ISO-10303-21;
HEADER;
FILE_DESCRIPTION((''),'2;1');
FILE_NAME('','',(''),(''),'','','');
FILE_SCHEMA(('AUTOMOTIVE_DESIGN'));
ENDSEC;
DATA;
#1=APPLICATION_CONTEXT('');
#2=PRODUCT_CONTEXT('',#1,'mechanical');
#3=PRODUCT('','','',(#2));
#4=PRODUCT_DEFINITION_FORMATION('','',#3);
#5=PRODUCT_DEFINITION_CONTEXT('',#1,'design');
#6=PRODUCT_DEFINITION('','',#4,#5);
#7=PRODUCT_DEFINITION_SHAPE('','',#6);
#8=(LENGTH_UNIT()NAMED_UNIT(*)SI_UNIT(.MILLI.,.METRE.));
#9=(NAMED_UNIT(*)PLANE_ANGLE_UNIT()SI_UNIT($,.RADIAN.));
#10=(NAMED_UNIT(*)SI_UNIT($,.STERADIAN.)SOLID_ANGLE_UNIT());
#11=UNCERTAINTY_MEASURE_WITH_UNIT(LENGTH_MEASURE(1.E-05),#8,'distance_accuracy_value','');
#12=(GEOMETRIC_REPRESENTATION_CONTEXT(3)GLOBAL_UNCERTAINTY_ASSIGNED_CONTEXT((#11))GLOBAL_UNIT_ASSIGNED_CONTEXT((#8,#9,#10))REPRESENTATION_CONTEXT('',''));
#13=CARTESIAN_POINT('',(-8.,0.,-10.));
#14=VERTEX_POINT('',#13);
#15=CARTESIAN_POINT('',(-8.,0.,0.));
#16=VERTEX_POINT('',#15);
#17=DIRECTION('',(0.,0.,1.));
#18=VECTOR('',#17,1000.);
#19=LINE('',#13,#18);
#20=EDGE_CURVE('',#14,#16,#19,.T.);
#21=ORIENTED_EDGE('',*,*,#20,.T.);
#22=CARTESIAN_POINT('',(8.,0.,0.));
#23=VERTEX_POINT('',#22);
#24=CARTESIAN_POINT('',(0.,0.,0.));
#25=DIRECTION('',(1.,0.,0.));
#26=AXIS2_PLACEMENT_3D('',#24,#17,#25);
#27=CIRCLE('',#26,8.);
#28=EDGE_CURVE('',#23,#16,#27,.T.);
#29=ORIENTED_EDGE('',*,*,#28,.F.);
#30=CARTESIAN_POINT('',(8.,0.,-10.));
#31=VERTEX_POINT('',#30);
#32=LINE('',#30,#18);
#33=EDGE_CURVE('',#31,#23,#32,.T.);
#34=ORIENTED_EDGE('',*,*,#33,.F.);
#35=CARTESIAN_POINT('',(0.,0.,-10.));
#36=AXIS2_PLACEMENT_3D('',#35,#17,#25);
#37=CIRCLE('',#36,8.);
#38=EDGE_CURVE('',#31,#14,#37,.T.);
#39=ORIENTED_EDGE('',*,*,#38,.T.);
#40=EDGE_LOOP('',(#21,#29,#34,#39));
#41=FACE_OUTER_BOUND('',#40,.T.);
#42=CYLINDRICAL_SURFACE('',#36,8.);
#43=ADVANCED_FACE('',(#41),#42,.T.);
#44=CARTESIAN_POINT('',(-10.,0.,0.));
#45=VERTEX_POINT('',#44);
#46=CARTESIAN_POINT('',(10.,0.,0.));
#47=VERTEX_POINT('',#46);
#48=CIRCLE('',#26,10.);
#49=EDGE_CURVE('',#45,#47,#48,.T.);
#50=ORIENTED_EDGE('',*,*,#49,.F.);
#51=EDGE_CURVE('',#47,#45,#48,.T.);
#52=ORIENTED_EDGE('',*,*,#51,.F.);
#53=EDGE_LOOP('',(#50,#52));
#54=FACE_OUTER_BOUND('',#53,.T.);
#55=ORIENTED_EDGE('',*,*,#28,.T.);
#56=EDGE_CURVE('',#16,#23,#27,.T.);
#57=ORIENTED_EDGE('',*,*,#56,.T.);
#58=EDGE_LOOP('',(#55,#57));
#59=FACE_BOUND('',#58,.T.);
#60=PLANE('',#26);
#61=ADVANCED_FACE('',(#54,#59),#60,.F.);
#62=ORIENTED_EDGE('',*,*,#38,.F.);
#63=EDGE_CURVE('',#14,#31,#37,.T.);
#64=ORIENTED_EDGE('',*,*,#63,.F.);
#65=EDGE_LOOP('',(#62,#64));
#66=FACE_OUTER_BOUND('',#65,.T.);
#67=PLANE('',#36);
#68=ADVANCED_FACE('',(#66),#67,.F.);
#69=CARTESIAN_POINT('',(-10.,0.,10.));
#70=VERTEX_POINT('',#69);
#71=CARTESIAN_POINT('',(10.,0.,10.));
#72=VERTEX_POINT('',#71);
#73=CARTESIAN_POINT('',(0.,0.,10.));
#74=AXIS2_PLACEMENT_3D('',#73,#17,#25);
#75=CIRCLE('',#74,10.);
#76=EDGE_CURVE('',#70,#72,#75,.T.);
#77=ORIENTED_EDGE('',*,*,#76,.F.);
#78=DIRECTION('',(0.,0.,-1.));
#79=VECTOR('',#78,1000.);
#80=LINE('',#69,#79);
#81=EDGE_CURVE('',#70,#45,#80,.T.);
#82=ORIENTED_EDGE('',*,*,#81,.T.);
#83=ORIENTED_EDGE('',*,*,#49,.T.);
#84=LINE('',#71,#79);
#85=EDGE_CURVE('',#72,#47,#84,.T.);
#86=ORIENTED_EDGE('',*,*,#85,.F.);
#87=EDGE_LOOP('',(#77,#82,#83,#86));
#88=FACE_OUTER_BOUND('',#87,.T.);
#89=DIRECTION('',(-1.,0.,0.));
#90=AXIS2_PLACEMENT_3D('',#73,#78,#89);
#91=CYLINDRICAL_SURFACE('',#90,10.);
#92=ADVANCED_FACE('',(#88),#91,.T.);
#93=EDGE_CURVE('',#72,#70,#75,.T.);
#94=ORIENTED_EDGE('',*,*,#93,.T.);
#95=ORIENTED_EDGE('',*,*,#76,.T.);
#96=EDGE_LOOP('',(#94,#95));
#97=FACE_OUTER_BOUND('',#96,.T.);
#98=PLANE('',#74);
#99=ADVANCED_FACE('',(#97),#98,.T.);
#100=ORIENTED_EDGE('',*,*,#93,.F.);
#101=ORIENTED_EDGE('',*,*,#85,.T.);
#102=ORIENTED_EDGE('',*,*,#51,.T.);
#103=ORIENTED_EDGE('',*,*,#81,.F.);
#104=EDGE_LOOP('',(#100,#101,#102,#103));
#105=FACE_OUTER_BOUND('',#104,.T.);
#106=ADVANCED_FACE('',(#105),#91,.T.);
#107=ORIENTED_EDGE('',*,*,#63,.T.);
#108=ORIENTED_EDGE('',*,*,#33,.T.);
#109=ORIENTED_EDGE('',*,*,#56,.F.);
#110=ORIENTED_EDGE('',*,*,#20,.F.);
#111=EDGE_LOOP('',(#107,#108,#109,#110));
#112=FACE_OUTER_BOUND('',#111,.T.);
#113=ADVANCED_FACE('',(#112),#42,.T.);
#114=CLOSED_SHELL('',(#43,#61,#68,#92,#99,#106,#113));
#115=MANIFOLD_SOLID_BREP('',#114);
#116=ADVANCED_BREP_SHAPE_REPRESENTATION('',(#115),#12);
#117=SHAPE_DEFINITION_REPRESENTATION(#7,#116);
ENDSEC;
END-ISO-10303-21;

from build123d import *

# Parameters (mm, degrees)
SKETCH_1_R      = 8
EXTRUDE_1_DEPTH = 10
SKETCH_2_R      = 10
EXTRUDE_2_DEPTH = 10


with BuildPart() as part:
    # 草图1 → 凸台-拉伸1 (new body)
    with BuildSketch(Plane.XY):
        Circle(SKETCH_1_R)
    extrude(amount=-EXTRUDE_1_DEPTH)

    # 草图2 → 凸台-拉伸2 (add)
    with BuildSketch(Plane.XY):
        Circle(SKETCH_2_R)
    extrude(amount=EXTRUDE_2_DEPTH)


solid = part.part
